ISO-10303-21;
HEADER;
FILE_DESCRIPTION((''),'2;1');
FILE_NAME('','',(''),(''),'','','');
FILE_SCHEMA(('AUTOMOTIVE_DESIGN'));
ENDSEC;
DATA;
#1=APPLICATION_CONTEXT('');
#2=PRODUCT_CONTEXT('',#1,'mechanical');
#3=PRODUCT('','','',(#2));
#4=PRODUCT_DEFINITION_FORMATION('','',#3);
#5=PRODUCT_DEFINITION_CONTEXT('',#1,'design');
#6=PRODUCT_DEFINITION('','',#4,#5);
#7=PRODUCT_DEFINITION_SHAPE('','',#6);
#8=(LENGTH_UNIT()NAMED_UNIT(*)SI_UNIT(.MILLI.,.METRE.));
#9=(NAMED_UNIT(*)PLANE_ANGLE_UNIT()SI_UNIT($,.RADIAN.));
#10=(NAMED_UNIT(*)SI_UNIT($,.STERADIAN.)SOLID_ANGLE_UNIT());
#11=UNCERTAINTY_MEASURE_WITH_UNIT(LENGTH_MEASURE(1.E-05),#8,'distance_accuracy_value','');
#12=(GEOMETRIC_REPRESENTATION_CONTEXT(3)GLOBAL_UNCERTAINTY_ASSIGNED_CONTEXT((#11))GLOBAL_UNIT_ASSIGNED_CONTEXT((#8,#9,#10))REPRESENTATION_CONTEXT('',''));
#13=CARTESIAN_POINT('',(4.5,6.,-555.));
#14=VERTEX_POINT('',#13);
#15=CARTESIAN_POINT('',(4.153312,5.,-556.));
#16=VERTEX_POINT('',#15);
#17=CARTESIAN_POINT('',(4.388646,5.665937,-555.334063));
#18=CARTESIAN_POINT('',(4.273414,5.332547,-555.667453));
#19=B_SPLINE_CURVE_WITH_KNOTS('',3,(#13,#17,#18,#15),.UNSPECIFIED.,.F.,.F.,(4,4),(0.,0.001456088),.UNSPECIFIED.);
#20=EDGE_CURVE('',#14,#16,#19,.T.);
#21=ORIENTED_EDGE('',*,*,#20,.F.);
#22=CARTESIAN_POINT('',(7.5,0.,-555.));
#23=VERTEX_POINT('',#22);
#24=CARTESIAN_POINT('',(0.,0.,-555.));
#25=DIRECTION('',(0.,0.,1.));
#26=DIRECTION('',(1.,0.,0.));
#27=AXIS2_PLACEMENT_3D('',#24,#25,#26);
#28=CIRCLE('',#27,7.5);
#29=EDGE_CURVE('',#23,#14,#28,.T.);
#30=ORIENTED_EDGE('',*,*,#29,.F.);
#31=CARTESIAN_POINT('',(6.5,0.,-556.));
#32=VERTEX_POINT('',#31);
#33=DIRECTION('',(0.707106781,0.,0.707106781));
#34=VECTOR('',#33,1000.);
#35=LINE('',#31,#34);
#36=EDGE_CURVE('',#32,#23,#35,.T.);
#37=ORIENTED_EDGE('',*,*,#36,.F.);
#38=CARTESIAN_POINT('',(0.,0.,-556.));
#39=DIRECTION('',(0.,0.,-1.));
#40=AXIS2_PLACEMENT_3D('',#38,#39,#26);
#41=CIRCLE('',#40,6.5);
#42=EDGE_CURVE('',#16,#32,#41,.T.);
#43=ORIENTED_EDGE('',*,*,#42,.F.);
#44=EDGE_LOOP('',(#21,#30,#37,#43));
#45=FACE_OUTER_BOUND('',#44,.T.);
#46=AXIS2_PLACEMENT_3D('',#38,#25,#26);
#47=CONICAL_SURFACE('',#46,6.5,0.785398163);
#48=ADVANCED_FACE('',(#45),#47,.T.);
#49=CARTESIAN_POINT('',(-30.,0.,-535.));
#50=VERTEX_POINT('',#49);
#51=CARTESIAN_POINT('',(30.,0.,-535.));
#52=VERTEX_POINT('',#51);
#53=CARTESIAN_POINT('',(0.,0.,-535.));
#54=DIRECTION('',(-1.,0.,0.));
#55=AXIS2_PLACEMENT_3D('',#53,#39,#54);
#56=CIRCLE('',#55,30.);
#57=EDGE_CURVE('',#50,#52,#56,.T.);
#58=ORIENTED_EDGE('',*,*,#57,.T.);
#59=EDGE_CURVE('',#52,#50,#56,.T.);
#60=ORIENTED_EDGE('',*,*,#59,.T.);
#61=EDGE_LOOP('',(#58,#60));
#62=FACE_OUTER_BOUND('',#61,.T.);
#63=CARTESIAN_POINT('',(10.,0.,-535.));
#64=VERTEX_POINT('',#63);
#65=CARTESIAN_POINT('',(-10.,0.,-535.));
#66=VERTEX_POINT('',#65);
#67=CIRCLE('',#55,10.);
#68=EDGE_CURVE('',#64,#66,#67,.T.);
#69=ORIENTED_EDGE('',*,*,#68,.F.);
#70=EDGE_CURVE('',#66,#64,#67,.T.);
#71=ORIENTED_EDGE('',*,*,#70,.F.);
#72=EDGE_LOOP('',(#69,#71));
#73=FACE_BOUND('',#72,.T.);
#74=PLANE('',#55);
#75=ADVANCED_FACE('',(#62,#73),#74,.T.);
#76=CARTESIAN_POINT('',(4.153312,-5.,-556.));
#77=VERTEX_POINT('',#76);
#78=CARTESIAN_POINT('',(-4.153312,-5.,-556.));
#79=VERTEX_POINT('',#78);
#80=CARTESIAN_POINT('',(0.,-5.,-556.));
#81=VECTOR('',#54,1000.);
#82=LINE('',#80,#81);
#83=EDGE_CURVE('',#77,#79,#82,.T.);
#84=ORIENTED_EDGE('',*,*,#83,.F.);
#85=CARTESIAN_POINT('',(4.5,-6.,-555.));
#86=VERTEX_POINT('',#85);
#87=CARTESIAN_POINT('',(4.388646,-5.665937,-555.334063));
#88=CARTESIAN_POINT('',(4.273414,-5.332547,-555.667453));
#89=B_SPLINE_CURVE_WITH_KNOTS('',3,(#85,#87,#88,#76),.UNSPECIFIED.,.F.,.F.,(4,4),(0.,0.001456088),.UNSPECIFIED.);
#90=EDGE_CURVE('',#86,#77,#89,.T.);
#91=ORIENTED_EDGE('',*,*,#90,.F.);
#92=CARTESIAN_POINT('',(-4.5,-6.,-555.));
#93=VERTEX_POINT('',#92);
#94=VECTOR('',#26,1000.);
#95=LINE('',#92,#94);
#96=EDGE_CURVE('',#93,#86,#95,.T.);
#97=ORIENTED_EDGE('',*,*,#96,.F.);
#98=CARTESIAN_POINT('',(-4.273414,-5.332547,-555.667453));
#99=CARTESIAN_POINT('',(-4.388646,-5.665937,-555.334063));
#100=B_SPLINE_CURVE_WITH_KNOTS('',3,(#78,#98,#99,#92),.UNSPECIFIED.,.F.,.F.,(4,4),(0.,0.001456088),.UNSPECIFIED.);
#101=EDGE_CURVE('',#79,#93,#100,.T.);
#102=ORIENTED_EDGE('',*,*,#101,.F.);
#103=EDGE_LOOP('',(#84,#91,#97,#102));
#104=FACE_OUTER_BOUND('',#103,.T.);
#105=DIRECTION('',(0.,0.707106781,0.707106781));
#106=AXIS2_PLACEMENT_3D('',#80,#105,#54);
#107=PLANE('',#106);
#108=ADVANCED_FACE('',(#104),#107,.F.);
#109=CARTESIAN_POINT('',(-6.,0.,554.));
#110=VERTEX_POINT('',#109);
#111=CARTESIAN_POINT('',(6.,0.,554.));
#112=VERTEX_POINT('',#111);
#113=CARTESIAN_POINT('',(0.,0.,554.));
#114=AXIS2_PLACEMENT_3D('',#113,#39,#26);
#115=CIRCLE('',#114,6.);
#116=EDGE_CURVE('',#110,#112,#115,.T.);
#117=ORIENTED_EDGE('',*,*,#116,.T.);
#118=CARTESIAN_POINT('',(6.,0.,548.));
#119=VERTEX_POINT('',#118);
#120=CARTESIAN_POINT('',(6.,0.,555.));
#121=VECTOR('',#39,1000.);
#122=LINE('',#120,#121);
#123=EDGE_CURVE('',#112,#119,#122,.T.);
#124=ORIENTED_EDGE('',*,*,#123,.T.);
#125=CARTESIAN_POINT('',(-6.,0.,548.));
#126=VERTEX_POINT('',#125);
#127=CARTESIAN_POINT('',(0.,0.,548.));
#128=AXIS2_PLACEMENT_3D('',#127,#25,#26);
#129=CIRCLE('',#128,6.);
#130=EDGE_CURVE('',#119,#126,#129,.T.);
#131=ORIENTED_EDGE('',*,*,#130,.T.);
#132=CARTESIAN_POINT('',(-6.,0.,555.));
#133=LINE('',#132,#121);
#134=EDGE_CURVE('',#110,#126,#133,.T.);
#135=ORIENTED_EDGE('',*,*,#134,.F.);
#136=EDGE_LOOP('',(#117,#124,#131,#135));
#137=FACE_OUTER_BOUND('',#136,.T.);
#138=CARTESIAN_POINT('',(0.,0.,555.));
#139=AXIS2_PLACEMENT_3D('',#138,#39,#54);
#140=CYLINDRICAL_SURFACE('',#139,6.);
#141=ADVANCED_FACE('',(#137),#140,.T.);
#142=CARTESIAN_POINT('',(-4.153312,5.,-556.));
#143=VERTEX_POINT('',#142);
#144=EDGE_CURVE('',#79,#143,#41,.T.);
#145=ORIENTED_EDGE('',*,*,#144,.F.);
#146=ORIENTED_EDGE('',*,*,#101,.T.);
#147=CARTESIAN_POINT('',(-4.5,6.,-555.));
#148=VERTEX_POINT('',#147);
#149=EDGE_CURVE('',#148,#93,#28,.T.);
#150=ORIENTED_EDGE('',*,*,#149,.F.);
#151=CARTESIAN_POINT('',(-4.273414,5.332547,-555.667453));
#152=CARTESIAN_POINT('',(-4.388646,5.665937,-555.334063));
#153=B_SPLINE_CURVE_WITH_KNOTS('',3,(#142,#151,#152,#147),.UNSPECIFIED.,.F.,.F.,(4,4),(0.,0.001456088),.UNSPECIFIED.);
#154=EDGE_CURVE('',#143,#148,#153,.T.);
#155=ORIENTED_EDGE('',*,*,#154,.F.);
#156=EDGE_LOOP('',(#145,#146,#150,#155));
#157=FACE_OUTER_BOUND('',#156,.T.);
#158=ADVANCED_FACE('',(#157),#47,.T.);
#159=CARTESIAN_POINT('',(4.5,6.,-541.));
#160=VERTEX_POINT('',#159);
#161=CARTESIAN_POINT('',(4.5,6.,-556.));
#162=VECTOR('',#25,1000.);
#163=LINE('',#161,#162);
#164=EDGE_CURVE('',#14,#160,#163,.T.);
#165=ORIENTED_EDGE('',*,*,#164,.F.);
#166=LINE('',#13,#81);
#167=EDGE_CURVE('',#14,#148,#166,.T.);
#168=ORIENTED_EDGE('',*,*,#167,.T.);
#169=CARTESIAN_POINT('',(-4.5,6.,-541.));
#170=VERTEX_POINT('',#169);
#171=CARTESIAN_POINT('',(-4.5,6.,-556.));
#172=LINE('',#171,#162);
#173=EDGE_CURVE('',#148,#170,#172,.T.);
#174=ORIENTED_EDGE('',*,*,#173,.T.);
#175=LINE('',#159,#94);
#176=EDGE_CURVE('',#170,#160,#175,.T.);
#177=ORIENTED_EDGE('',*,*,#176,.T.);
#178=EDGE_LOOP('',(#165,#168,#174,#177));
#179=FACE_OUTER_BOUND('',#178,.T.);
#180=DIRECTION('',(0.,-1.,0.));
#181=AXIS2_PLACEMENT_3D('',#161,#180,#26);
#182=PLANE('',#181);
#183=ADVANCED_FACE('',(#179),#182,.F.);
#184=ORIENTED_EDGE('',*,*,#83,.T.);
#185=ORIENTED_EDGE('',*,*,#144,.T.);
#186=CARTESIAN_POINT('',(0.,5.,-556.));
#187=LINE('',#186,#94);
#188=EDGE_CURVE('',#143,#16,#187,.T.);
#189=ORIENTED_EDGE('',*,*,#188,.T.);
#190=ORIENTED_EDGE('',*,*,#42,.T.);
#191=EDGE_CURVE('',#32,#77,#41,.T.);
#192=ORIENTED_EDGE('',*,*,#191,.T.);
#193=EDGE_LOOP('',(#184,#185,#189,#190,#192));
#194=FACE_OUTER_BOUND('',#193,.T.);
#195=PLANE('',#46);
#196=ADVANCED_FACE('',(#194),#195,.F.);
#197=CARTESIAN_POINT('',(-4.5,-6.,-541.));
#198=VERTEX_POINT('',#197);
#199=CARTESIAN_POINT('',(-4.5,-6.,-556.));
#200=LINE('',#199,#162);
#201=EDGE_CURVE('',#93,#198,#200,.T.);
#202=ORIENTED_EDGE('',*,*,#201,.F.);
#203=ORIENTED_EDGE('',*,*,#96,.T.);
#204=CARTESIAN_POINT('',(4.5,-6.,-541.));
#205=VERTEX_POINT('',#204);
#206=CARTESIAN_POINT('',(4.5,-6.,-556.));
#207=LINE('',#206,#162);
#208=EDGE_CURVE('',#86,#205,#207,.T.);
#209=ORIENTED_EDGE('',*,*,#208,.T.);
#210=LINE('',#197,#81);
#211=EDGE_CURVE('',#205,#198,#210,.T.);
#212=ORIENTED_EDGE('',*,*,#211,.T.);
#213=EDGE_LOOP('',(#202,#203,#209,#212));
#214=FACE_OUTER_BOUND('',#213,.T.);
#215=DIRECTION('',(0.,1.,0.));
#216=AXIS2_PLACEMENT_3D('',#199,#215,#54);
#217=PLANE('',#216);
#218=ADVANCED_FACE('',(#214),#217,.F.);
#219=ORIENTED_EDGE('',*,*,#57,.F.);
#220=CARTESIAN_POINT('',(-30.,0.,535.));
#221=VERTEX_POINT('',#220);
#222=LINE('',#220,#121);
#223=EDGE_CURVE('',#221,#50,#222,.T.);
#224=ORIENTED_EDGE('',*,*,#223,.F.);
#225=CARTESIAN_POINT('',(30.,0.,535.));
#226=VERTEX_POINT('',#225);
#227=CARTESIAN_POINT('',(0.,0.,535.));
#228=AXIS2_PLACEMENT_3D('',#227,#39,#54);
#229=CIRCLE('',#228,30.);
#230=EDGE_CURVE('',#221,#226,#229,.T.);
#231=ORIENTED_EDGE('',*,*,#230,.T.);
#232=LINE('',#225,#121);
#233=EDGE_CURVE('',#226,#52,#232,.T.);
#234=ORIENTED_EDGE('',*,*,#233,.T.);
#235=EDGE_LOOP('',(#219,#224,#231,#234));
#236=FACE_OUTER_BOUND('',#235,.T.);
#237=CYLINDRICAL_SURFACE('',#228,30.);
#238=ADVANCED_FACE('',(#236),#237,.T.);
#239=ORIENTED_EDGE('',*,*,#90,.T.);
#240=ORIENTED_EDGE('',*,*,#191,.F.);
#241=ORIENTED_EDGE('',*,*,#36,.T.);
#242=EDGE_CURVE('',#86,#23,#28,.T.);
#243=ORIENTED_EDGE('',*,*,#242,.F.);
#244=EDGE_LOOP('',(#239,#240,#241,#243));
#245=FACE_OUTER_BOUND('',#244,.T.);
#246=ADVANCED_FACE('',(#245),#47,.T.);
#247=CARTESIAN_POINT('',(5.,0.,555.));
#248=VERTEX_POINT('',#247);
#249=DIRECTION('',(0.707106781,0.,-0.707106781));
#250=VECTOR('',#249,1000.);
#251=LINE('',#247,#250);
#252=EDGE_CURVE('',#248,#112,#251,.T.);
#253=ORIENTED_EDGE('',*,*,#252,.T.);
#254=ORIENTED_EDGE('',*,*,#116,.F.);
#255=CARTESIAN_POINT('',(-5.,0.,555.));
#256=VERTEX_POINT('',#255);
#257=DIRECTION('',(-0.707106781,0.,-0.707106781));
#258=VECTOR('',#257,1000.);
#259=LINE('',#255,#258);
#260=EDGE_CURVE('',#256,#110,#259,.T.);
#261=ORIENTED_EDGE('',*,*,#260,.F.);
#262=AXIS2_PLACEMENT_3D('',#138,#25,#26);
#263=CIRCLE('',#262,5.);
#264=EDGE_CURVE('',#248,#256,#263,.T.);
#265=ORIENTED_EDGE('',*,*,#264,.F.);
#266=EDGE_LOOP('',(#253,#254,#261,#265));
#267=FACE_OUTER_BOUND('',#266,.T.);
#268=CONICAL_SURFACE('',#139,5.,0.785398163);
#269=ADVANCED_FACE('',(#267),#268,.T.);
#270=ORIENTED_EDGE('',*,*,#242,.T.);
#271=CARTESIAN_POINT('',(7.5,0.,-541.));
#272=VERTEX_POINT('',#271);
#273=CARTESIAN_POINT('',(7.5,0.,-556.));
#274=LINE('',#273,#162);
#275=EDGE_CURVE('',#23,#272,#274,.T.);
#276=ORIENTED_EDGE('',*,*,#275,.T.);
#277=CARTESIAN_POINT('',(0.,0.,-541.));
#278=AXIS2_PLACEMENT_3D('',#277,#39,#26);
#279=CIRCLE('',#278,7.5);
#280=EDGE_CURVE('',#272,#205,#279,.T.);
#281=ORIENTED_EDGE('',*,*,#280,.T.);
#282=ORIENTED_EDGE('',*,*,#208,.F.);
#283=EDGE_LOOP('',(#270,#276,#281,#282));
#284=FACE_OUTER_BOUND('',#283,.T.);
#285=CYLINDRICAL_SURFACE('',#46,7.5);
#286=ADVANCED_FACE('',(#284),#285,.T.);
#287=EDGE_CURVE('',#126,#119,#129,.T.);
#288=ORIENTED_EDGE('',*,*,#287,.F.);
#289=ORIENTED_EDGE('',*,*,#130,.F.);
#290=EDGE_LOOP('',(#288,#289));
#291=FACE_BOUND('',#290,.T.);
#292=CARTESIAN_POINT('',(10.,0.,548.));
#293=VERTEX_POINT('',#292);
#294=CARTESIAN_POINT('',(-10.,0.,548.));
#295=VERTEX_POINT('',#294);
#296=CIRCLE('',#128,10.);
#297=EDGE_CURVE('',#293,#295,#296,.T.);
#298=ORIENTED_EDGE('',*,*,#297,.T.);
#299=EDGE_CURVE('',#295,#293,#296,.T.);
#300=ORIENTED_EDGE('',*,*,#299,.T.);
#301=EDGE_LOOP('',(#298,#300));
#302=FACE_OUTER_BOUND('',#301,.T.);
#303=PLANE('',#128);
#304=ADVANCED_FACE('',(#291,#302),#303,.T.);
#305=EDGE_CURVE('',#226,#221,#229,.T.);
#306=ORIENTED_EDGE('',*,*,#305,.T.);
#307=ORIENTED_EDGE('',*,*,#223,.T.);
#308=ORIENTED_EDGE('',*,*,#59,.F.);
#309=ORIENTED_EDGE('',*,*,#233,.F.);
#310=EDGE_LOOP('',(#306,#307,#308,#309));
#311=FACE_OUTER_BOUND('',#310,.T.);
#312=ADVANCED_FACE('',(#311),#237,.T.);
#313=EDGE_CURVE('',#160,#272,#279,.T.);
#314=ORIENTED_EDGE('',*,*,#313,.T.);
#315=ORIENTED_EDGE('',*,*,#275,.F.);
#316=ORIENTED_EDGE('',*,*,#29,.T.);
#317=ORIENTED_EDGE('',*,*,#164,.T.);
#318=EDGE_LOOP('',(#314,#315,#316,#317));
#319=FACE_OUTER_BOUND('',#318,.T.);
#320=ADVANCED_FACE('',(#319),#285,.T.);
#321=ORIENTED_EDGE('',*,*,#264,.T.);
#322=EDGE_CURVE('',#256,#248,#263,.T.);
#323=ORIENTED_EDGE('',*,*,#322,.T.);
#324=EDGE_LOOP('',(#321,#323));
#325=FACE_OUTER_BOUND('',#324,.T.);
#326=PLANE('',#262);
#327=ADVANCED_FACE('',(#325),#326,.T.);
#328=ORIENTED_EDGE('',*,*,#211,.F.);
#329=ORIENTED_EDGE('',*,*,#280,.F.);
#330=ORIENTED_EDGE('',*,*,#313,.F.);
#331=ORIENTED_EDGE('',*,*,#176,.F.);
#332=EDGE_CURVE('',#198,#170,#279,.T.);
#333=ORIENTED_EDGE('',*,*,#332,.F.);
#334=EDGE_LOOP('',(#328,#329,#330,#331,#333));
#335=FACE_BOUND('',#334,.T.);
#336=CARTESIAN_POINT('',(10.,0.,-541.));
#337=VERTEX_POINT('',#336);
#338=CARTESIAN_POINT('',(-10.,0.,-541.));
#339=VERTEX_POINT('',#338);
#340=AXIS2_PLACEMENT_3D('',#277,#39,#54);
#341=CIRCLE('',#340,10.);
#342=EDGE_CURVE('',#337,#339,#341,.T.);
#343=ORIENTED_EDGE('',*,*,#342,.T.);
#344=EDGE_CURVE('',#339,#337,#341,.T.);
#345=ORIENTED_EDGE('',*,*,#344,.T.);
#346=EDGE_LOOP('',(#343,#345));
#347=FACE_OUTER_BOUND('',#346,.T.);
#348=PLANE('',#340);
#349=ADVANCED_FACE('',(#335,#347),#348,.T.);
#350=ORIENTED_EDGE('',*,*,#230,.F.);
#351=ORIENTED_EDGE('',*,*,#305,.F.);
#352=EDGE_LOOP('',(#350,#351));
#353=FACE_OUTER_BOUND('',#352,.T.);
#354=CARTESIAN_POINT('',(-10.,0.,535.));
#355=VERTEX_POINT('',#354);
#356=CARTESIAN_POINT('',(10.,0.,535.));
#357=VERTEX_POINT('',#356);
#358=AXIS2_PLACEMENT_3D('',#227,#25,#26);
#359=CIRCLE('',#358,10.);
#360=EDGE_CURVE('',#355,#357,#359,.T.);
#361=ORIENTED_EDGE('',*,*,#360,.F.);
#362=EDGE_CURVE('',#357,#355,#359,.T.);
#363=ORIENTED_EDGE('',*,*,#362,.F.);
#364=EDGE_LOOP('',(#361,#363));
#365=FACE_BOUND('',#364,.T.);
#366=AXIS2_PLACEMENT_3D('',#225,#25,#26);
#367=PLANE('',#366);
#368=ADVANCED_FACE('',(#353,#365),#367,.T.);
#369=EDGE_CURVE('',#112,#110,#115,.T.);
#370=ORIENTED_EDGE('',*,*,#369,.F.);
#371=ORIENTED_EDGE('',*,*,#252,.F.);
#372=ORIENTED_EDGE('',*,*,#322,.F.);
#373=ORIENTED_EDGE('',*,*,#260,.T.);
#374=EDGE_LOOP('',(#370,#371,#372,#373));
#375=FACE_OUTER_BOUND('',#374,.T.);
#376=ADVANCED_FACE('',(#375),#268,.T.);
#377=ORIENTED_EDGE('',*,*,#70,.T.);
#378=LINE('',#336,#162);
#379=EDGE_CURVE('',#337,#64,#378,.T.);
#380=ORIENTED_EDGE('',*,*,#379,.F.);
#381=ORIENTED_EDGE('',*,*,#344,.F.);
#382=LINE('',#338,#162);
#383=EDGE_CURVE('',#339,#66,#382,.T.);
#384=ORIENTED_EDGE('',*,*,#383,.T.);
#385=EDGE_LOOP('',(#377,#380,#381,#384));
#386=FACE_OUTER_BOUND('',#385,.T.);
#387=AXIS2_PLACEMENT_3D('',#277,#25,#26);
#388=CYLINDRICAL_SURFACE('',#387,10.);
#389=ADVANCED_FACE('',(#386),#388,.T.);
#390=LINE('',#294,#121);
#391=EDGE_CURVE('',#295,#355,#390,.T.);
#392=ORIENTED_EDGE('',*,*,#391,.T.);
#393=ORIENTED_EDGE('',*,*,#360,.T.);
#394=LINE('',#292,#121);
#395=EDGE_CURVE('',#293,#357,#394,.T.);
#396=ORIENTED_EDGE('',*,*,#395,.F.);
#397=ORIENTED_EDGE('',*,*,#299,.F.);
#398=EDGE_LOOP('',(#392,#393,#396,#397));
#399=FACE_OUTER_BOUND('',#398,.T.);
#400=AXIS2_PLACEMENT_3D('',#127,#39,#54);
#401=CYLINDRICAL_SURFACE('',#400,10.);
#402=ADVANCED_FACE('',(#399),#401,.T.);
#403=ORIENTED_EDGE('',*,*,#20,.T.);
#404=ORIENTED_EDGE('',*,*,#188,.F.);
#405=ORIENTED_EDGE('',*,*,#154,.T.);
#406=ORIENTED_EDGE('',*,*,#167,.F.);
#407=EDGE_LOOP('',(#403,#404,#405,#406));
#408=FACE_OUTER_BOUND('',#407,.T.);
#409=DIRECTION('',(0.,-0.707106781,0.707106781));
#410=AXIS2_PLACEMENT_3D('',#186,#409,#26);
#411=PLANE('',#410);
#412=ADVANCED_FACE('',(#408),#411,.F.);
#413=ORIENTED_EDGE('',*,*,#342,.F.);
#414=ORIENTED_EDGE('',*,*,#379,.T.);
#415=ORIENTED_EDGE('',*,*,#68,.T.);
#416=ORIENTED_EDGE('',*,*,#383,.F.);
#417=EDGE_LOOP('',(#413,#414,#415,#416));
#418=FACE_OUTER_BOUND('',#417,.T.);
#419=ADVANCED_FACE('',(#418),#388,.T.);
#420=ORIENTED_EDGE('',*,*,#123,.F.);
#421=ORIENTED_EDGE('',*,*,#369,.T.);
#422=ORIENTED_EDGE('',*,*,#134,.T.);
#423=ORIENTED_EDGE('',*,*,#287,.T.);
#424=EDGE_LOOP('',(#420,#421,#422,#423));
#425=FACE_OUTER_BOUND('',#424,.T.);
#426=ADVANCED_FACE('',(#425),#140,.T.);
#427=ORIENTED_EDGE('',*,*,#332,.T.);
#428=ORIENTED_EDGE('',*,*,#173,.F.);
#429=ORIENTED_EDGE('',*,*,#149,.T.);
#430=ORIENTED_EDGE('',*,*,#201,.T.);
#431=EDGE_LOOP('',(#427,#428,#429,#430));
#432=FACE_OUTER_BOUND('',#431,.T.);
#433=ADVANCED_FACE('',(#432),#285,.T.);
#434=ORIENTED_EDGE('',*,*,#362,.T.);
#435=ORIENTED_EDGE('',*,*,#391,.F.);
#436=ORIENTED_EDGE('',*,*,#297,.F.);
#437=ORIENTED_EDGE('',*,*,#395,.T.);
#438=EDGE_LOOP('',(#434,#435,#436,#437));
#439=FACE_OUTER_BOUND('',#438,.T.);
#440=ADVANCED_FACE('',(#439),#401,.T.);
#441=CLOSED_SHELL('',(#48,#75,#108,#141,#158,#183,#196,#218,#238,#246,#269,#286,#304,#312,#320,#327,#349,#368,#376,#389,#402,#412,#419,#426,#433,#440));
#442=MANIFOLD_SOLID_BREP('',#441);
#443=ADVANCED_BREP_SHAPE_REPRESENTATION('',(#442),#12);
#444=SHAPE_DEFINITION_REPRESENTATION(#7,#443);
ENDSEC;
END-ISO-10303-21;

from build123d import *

# Parameters (mm, degrees)
SKETCH1_W           = 30
SKETCH1_H           = 1070
SKETCH2_R           = 10
BOSS_EXTRUDE1_DEPTH = 6
BOSS_EXTRUDE2_DEPTH = 15
BOSS_EXTRUDE3_START = 13
SKETCH4_R           = 10
BOSS_EXTRUDE3_DEPTH = 13
SKETCH5_R           = 6
BOSS_EXTRUDE4_DEPTH = 7
CHAMFER1_SIZE       = 1


with BuildPart() as part:
    # Sketch1 → Revolve1 (revolve)
    with BuildSketch(Plane.XZ, mode=Mode.PRIVATE) as revolve1_sk:
        with Locations((15, 0)):
            Rectangle(SKETCH1_W, SKETCH1_H)
    revolve(revolve1_sk.sketch.rotate(Axis((0, 0, 535), (0, 0, -1)), 180), axis=Axis((0, 0, 535), (0, 0, -1)))

    # Sketch2 → Boss-Extrude1 (add)
    with BuildSketch(Plane(origin=(0, 0, -535), x_dir=(-1, 0, 0), z_dir=(0, 0, -1))):
        Circle(SKETCH2_R)
    extrude(amount=BOSS_EXTRUDE1_DEPTH)

    # Sketch3 → Boss-Extrude2 (add)
    with BuildSketch(Plane(origin=(0, 0, -541), x_dir=(-1, 0, 0), z_dir=(0, 0, -1))):
        with BuildLine():
            Line((-4.5, 6), (4.5, 6))
            ThreePointArc((4.5, 6), (7.5, 0), (4.5, -6))
            Line((4.5, -6), (-4.5, -6))
            ThreePointArc((-4.5, -6), (-7.5, 0), (-4.5, 6))
        make_face()
    extrude(amount=BOSS_EXTRUDE2_DEPTH)

    # Sketch4 → Boss-Extrude3 (add)
    with BuildSketch(Plane.XY.offset(535).offset(BOSS_EXTRUDE3_START)):
        with Locations(Location((0, 0, 0), (0, 0, 180))):
            Circle(SKETCH4_R)
    extrude(amount=-BOSS_EXTRUDE3_DEPTH)

    # Sketch5 → Boss-Extrude4 (add)
    with BuildSketch(Plane.XY.offset(548)):
        with Locations(Location((0, 0, 0), (0, 0, 180))):
            Circle(SKETCH5_R)
    extrude(amount=BOSS_EXTRUDE4_DEPTH)

    # Chamfer1
    chamfer1_edges = [part.edges().sort_by_distance(p)[0] for p in [
        (7.5, 0, -556),
        (0, -6, -556),
        (-7.5, 0, -556),
        (0, 6, -556),
        (6, 0, 555),
    ]]
    chamfer(chamfer1_edges, length=CHAMFER1_SIZE)


solid = part.part
